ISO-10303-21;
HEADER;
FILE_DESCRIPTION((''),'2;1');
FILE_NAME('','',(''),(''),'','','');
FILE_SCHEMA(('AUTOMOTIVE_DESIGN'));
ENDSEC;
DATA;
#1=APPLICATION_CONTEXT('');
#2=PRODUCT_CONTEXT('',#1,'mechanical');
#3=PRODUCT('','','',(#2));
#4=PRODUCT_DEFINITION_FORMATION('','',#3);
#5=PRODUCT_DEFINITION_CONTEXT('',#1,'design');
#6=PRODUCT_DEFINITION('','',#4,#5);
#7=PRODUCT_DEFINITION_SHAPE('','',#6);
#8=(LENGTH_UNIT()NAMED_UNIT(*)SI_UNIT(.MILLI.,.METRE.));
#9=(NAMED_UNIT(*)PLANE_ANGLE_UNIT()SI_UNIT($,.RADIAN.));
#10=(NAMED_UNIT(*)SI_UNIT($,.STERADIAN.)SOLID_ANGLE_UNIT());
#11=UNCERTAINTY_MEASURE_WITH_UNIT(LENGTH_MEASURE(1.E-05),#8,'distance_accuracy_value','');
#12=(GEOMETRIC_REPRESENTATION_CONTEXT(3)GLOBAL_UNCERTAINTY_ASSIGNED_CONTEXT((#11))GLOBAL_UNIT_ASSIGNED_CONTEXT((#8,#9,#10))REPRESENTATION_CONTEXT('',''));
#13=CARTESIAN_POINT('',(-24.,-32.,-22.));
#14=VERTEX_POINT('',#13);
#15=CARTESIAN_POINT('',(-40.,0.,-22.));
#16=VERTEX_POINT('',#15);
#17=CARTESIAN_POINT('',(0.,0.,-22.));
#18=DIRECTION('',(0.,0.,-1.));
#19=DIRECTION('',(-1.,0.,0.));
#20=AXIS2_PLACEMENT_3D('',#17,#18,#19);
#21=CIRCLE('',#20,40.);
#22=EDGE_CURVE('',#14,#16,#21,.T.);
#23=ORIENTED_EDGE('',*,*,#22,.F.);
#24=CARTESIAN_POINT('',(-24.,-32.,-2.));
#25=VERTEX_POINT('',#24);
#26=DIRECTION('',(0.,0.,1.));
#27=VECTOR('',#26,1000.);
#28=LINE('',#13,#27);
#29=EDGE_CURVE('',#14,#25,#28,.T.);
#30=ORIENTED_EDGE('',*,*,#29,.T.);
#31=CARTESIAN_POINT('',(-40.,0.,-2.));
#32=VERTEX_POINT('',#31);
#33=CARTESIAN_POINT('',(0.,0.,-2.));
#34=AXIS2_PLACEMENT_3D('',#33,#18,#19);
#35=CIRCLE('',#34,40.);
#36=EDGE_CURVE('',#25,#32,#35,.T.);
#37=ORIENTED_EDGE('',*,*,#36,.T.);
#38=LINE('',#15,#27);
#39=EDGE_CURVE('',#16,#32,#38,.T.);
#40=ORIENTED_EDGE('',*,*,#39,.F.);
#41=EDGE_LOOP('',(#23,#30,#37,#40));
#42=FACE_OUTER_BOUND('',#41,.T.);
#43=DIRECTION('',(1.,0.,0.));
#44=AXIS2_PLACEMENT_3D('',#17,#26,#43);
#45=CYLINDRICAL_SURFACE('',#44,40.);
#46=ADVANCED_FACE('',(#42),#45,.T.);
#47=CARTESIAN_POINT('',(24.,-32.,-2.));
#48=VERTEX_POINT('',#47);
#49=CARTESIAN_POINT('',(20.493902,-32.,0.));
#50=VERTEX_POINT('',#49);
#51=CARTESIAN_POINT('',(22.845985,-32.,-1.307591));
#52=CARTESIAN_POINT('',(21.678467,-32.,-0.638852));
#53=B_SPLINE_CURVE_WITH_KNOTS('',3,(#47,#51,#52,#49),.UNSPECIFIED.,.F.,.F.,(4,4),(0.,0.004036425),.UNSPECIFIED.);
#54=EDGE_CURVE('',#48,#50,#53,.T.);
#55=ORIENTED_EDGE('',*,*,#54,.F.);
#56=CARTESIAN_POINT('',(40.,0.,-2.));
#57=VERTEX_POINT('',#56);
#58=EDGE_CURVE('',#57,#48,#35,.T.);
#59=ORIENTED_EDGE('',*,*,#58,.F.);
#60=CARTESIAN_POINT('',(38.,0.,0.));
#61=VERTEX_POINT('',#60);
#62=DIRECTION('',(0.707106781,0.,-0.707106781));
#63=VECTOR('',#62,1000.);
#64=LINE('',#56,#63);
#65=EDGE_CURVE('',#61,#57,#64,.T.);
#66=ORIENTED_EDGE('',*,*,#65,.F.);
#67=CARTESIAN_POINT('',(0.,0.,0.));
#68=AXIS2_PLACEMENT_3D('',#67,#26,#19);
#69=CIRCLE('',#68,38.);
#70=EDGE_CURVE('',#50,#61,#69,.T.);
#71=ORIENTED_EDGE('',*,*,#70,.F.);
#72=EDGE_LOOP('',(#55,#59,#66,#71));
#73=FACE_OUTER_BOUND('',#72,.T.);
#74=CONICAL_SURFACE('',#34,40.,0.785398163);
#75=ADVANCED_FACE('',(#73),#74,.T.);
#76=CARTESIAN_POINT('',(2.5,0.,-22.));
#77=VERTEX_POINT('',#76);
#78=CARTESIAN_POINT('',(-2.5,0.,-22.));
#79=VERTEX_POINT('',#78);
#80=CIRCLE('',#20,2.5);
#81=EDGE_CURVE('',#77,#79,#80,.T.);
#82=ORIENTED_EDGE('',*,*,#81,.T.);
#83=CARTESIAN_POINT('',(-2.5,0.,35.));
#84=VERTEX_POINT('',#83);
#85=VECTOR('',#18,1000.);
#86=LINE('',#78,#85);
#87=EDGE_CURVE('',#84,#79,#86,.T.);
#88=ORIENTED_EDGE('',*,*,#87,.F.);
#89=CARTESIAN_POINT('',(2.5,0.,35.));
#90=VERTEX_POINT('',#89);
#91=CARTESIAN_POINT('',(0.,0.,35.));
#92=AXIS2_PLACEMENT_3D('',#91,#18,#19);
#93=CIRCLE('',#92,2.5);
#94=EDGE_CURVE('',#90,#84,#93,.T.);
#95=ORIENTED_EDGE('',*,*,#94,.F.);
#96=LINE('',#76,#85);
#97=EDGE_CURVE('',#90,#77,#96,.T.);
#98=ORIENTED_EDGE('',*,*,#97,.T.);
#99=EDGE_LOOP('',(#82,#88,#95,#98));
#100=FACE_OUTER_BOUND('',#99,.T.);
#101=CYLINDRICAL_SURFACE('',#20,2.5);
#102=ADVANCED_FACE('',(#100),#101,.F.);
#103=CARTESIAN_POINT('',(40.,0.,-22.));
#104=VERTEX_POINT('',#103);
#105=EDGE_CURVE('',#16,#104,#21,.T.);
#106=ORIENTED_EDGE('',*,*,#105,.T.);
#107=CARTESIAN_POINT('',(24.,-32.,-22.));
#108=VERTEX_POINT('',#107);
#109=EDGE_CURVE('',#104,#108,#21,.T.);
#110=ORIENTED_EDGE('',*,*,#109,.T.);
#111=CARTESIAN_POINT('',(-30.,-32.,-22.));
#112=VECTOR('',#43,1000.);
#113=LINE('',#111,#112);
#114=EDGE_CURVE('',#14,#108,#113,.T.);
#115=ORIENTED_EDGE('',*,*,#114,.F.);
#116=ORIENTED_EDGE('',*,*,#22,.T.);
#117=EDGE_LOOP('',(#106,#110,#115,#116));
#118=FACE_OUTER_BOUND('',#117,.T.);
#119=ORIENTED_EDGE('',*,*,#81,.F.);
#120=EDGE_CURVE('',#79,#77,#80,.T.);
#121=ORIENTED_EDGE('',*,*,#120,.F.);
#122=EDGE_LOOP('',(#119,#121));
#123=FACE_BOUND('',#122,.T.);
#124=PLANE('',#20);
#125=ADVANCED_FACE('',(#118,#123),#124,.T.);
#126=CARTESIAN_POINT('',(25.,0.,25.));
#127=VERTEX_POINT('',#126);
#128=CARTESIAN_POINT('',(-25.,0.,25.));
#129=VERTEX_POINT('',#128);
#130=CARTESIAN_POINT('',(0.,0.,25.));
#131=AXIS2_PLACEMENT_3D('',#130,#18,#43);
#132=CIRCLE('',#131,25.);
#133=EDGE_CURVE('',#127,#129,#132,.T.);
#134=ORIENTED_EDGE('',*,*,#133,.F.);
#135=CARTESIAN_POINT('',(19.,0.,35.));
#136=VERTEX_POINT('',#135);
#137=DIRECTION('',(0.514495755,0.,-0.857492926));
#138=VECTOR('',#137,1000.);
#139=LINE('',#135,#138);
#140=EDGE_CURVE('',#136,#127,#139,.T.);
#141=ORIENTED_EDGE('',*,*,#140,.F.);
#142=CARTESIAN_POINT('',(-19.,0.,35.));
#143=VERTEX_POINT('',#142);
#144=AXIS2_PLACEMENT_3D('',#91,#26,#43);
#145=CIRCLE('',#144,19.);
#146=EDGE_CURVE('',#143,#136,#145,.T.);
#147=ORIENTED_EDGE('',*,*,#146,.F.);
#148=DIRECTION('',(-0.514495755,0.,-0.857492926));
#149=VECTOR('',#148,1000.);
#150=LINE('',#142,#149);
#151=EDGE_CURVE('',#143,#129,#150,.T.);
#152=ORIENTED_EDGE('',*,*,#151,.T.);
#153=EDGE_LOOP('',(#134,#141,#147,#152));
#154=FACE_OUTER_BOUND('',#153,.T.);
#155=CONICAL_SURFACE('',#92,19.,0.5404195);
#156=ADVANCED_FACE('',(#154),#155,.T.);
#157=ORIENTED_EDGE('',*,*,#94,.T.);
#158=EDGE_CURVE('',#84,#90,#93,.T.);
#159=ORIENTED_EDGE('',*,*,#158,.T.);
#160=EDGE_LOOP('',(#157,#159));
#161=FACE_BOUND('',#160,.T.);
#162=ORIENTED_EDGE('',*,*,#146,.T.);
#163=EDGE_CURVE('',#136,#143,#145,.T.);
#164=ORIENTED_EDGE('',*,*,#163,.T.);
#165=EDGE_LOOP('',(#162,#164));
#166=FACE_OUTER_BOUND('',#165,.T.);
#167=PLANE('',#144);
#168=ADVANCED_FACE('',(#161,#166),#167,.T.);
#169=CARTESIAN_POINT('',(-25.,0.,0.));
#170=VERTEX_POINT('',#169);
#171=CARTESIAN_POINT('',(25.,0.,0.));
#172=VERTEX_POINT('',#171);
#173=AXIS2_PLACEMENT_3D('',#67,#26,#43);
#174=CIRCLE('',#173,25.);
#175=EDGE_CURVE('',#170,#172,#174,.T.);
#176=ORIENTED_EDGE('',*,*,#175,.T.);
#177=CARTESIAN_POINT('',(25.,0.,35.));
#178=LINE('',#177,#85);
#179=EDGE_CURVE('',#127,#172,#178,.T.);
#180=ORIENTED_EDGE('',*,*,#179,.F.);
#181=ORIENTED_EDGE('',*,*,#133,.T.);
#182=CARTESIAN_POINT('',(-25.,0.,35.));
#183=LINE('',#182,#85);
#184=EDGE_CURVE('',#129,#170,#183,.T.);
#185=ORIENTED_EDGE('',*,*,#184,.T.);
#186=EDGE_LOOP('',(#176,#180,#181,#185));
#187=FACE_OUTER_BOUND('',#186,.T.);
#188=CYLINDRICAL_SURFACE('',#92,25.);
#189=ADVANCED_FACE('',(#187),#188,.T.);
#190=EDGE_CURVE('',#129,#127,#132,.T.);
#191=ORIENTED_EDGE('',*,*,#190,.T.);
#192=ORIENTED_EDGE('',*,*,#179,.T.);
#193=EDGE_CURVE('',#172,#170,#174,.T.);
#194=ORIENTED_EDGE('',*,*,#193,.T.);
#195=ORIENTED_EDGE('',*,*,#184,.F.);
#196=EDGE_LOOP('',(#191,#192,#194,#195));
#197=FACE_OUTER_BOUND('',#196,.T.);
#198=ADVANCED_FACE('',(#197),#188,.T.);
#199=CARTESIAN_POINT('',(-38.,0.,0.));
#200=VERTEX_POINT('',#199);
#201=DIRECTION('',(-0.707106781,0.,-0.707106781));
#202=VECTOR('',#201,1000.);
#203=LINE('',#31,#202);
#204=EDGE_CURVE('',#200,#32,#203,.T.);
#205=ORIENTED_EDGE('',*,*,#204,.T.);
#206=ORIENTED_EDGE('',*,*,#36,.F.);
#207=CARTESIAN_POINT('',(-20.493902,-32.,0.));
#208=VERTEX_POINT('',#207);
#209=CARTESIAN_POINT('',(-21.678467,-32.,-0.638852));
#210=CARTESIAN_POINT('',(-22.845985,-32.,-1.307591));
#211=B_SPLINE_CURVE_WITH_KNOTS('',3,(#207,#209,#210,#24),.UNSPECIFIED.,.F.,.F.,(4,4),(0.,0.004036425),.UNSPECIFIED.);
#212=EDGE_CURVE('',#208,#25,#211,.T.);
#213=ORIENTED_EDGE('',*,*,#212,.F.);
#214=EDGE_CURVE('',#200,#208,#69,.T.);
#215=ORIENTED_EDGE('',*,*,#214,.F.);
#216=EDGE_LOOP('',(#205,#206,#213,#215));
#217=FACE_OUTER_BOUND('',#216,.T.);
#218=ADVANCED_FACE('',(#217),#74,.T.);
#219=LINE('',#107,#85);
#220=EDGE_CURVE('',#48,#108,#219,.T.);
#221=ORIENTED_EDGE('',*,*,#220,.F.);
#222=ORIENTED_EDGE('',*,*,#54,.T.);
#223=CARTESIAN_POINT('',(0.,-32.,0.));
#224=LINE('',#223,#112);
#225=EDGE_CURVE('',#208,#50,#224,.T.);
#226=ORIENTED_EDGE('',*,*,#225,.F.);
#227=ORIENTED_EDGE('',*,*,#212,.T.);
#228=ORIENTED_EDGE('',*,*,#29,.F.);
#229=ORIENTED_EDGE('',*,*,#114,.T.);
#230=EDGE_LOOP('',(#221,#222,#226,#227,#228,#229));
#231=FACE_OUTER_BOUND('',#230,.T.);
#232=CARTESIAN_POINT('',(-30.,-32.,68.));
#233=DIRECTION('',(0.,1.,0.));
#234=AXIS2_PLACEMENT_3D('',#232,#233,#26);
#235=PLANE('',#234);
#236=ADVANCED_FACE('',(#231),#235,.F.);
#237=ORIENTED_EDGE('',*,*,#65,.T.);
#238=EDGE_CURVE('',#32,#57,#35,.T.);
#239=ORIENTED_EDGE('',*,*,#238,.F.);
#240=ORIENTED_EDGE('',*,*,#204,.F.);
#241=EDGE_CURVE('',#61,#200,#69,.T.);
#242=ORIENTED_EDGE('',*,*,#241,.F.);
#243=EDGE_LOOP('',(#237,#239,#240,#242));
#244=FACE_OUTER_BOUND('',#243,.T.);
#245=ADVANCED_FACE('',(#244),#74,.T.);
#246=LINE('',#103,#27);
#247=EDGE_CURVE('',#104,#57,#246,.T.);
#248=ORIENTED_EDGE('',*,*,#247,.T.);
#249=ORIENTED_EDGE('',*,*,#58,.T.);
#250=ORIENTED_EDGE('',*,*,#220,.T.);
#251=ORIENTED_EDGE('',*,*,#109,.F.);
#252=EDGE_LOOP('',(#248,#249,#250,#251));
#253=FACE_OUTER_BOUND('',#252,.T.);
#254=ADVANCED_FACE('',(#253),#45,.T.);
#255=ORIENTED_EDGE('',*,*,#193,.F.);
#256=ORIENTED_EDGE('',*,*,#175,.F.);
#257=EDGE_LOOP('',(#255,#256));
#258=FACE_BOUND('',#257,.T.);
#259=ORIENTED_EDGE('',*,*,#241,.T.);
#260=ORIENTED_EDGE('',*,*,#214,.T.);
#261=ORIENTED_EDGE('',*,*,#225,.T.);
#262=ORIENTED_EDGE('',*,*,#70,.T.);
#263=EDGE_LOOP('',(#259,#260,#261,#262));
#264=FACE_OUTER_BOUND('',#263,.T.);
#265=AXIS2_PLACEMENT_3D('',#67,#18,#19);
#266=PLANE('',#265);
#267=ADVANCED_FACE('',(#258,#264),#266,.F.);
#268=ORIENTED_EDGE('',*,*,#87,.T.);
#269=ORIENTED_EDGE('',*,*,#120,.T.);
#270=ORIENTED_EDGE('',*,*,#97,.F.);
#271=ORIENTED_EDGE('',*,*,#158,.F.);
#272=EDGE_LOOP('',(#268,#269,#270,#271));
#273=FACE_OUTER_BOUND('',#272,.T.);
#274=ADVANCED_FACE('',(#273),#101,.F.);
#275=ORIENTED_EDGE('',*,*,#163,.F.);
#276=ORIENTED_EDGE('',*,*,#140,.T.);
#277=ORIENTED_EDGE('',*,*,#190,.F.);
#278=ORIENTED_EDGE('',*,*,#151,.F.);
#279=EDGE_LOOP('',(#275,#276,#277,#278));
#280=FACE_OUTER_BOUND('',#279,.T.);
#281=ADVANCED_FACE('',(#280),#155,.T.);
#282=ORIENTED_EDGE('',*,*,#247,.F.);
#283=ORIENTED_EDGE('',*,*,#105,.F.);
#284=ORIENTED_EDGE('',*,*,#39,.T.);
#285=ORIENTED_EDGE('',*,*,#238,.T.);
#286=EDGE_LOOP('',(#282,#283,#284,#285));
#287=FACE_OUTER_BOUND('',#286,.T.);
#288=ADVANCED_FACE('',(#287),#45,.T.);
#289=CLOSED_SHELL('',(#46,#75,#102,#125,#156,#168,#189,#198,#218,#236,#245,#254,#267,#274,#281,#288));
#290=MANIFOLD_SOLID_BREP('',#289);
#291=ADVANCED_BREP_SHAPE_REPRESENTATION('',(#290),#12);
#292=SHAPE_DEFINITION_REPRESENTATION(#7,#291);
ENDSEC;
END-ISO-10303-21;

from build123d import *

# Parameters (mm, degrees)
SKETCH1_R           = 25
BOSS_EXTRUDE1_DEPTH = 35
CHAMFER1_SIZE       = 10
CHAMFER1_SIZE2      = 6
SKETCH2_R           = 40
BOSS_EXTRUDE2_DEPTH = 22
SKETCH3_W           = 90
SKETCH3_H           = 30
CUT_EXTRUDE1_DEPTH  = 30
CHAMFER2_SIZE       = 2
M6_TAPPED_HOLE1_D   = 5


with BuildPart() as part:
    # Sketch1 → Boss-Extrude1 (new body)
    with BuildSketch(Plane.XY):
        Circle(SKETCH1_R)
    extrude(amount=BOSS_EXTRUDE1_DEPTH)

    # Chamfer1
    chamfer1_edges = [part.edges().sort_by_distance(p)[0] for p in [
        (-25, 0, 35),
    ]]
    chamfer1_side = [part.faces().sort_by_distance(p)[0] for p in [
        (-25, 0, 17.5),
    ]]
    chamfer(chamfer1_edges, length=CHAMFER1_SIZE, length2=CHAMFER1_SIZE2, reference=chamfer1_side[0])

    # Sketch2 → Boss-Extrude2 (add)
    with BuildSketch(Plane(origin=(0, 0, 0), x_dir=(-1, 0, 0), z_dir=(0, 0, -1))):
        Circle(SKETCH2_R)
    extrude(amount=BOSS_EXTRUDE2_DEPTH)

    # Sketch3 → Cut-Extrude1 (cut, symmetric)
    with BuildSketch(Plane(origin=(0, 0, 0), x_dir=(0, 0, -1), z_dir=(1, 0, 0))):
        with Locations((-23, -47)):
            Rectangle(SKETCH3_W, SKETCH3_H)
    extrude(amount=CUT_EXTRUDE1_DEPTH, both=True, mode=Mode.SUBTRACT)

    # Chamfer2
    chamfer2_edges = [part.edges().sort_by_distance(p)[0] for p in [
        (0, 40, 0),
    ]]
    chamfer(chamfer2_edges, length=CHAMFER2_SIZE)

    # M6 Tapped Hole1 (through all)
    with Locations(Plane(origin=(0, 0, -22), x_dir=(-1, 0, 0), z_dir=(0, 0, -1))):
        with Locations((0, 0)):
            Hole(M6_TAPPED_HOLE1_D / 2)


solid = part.part
